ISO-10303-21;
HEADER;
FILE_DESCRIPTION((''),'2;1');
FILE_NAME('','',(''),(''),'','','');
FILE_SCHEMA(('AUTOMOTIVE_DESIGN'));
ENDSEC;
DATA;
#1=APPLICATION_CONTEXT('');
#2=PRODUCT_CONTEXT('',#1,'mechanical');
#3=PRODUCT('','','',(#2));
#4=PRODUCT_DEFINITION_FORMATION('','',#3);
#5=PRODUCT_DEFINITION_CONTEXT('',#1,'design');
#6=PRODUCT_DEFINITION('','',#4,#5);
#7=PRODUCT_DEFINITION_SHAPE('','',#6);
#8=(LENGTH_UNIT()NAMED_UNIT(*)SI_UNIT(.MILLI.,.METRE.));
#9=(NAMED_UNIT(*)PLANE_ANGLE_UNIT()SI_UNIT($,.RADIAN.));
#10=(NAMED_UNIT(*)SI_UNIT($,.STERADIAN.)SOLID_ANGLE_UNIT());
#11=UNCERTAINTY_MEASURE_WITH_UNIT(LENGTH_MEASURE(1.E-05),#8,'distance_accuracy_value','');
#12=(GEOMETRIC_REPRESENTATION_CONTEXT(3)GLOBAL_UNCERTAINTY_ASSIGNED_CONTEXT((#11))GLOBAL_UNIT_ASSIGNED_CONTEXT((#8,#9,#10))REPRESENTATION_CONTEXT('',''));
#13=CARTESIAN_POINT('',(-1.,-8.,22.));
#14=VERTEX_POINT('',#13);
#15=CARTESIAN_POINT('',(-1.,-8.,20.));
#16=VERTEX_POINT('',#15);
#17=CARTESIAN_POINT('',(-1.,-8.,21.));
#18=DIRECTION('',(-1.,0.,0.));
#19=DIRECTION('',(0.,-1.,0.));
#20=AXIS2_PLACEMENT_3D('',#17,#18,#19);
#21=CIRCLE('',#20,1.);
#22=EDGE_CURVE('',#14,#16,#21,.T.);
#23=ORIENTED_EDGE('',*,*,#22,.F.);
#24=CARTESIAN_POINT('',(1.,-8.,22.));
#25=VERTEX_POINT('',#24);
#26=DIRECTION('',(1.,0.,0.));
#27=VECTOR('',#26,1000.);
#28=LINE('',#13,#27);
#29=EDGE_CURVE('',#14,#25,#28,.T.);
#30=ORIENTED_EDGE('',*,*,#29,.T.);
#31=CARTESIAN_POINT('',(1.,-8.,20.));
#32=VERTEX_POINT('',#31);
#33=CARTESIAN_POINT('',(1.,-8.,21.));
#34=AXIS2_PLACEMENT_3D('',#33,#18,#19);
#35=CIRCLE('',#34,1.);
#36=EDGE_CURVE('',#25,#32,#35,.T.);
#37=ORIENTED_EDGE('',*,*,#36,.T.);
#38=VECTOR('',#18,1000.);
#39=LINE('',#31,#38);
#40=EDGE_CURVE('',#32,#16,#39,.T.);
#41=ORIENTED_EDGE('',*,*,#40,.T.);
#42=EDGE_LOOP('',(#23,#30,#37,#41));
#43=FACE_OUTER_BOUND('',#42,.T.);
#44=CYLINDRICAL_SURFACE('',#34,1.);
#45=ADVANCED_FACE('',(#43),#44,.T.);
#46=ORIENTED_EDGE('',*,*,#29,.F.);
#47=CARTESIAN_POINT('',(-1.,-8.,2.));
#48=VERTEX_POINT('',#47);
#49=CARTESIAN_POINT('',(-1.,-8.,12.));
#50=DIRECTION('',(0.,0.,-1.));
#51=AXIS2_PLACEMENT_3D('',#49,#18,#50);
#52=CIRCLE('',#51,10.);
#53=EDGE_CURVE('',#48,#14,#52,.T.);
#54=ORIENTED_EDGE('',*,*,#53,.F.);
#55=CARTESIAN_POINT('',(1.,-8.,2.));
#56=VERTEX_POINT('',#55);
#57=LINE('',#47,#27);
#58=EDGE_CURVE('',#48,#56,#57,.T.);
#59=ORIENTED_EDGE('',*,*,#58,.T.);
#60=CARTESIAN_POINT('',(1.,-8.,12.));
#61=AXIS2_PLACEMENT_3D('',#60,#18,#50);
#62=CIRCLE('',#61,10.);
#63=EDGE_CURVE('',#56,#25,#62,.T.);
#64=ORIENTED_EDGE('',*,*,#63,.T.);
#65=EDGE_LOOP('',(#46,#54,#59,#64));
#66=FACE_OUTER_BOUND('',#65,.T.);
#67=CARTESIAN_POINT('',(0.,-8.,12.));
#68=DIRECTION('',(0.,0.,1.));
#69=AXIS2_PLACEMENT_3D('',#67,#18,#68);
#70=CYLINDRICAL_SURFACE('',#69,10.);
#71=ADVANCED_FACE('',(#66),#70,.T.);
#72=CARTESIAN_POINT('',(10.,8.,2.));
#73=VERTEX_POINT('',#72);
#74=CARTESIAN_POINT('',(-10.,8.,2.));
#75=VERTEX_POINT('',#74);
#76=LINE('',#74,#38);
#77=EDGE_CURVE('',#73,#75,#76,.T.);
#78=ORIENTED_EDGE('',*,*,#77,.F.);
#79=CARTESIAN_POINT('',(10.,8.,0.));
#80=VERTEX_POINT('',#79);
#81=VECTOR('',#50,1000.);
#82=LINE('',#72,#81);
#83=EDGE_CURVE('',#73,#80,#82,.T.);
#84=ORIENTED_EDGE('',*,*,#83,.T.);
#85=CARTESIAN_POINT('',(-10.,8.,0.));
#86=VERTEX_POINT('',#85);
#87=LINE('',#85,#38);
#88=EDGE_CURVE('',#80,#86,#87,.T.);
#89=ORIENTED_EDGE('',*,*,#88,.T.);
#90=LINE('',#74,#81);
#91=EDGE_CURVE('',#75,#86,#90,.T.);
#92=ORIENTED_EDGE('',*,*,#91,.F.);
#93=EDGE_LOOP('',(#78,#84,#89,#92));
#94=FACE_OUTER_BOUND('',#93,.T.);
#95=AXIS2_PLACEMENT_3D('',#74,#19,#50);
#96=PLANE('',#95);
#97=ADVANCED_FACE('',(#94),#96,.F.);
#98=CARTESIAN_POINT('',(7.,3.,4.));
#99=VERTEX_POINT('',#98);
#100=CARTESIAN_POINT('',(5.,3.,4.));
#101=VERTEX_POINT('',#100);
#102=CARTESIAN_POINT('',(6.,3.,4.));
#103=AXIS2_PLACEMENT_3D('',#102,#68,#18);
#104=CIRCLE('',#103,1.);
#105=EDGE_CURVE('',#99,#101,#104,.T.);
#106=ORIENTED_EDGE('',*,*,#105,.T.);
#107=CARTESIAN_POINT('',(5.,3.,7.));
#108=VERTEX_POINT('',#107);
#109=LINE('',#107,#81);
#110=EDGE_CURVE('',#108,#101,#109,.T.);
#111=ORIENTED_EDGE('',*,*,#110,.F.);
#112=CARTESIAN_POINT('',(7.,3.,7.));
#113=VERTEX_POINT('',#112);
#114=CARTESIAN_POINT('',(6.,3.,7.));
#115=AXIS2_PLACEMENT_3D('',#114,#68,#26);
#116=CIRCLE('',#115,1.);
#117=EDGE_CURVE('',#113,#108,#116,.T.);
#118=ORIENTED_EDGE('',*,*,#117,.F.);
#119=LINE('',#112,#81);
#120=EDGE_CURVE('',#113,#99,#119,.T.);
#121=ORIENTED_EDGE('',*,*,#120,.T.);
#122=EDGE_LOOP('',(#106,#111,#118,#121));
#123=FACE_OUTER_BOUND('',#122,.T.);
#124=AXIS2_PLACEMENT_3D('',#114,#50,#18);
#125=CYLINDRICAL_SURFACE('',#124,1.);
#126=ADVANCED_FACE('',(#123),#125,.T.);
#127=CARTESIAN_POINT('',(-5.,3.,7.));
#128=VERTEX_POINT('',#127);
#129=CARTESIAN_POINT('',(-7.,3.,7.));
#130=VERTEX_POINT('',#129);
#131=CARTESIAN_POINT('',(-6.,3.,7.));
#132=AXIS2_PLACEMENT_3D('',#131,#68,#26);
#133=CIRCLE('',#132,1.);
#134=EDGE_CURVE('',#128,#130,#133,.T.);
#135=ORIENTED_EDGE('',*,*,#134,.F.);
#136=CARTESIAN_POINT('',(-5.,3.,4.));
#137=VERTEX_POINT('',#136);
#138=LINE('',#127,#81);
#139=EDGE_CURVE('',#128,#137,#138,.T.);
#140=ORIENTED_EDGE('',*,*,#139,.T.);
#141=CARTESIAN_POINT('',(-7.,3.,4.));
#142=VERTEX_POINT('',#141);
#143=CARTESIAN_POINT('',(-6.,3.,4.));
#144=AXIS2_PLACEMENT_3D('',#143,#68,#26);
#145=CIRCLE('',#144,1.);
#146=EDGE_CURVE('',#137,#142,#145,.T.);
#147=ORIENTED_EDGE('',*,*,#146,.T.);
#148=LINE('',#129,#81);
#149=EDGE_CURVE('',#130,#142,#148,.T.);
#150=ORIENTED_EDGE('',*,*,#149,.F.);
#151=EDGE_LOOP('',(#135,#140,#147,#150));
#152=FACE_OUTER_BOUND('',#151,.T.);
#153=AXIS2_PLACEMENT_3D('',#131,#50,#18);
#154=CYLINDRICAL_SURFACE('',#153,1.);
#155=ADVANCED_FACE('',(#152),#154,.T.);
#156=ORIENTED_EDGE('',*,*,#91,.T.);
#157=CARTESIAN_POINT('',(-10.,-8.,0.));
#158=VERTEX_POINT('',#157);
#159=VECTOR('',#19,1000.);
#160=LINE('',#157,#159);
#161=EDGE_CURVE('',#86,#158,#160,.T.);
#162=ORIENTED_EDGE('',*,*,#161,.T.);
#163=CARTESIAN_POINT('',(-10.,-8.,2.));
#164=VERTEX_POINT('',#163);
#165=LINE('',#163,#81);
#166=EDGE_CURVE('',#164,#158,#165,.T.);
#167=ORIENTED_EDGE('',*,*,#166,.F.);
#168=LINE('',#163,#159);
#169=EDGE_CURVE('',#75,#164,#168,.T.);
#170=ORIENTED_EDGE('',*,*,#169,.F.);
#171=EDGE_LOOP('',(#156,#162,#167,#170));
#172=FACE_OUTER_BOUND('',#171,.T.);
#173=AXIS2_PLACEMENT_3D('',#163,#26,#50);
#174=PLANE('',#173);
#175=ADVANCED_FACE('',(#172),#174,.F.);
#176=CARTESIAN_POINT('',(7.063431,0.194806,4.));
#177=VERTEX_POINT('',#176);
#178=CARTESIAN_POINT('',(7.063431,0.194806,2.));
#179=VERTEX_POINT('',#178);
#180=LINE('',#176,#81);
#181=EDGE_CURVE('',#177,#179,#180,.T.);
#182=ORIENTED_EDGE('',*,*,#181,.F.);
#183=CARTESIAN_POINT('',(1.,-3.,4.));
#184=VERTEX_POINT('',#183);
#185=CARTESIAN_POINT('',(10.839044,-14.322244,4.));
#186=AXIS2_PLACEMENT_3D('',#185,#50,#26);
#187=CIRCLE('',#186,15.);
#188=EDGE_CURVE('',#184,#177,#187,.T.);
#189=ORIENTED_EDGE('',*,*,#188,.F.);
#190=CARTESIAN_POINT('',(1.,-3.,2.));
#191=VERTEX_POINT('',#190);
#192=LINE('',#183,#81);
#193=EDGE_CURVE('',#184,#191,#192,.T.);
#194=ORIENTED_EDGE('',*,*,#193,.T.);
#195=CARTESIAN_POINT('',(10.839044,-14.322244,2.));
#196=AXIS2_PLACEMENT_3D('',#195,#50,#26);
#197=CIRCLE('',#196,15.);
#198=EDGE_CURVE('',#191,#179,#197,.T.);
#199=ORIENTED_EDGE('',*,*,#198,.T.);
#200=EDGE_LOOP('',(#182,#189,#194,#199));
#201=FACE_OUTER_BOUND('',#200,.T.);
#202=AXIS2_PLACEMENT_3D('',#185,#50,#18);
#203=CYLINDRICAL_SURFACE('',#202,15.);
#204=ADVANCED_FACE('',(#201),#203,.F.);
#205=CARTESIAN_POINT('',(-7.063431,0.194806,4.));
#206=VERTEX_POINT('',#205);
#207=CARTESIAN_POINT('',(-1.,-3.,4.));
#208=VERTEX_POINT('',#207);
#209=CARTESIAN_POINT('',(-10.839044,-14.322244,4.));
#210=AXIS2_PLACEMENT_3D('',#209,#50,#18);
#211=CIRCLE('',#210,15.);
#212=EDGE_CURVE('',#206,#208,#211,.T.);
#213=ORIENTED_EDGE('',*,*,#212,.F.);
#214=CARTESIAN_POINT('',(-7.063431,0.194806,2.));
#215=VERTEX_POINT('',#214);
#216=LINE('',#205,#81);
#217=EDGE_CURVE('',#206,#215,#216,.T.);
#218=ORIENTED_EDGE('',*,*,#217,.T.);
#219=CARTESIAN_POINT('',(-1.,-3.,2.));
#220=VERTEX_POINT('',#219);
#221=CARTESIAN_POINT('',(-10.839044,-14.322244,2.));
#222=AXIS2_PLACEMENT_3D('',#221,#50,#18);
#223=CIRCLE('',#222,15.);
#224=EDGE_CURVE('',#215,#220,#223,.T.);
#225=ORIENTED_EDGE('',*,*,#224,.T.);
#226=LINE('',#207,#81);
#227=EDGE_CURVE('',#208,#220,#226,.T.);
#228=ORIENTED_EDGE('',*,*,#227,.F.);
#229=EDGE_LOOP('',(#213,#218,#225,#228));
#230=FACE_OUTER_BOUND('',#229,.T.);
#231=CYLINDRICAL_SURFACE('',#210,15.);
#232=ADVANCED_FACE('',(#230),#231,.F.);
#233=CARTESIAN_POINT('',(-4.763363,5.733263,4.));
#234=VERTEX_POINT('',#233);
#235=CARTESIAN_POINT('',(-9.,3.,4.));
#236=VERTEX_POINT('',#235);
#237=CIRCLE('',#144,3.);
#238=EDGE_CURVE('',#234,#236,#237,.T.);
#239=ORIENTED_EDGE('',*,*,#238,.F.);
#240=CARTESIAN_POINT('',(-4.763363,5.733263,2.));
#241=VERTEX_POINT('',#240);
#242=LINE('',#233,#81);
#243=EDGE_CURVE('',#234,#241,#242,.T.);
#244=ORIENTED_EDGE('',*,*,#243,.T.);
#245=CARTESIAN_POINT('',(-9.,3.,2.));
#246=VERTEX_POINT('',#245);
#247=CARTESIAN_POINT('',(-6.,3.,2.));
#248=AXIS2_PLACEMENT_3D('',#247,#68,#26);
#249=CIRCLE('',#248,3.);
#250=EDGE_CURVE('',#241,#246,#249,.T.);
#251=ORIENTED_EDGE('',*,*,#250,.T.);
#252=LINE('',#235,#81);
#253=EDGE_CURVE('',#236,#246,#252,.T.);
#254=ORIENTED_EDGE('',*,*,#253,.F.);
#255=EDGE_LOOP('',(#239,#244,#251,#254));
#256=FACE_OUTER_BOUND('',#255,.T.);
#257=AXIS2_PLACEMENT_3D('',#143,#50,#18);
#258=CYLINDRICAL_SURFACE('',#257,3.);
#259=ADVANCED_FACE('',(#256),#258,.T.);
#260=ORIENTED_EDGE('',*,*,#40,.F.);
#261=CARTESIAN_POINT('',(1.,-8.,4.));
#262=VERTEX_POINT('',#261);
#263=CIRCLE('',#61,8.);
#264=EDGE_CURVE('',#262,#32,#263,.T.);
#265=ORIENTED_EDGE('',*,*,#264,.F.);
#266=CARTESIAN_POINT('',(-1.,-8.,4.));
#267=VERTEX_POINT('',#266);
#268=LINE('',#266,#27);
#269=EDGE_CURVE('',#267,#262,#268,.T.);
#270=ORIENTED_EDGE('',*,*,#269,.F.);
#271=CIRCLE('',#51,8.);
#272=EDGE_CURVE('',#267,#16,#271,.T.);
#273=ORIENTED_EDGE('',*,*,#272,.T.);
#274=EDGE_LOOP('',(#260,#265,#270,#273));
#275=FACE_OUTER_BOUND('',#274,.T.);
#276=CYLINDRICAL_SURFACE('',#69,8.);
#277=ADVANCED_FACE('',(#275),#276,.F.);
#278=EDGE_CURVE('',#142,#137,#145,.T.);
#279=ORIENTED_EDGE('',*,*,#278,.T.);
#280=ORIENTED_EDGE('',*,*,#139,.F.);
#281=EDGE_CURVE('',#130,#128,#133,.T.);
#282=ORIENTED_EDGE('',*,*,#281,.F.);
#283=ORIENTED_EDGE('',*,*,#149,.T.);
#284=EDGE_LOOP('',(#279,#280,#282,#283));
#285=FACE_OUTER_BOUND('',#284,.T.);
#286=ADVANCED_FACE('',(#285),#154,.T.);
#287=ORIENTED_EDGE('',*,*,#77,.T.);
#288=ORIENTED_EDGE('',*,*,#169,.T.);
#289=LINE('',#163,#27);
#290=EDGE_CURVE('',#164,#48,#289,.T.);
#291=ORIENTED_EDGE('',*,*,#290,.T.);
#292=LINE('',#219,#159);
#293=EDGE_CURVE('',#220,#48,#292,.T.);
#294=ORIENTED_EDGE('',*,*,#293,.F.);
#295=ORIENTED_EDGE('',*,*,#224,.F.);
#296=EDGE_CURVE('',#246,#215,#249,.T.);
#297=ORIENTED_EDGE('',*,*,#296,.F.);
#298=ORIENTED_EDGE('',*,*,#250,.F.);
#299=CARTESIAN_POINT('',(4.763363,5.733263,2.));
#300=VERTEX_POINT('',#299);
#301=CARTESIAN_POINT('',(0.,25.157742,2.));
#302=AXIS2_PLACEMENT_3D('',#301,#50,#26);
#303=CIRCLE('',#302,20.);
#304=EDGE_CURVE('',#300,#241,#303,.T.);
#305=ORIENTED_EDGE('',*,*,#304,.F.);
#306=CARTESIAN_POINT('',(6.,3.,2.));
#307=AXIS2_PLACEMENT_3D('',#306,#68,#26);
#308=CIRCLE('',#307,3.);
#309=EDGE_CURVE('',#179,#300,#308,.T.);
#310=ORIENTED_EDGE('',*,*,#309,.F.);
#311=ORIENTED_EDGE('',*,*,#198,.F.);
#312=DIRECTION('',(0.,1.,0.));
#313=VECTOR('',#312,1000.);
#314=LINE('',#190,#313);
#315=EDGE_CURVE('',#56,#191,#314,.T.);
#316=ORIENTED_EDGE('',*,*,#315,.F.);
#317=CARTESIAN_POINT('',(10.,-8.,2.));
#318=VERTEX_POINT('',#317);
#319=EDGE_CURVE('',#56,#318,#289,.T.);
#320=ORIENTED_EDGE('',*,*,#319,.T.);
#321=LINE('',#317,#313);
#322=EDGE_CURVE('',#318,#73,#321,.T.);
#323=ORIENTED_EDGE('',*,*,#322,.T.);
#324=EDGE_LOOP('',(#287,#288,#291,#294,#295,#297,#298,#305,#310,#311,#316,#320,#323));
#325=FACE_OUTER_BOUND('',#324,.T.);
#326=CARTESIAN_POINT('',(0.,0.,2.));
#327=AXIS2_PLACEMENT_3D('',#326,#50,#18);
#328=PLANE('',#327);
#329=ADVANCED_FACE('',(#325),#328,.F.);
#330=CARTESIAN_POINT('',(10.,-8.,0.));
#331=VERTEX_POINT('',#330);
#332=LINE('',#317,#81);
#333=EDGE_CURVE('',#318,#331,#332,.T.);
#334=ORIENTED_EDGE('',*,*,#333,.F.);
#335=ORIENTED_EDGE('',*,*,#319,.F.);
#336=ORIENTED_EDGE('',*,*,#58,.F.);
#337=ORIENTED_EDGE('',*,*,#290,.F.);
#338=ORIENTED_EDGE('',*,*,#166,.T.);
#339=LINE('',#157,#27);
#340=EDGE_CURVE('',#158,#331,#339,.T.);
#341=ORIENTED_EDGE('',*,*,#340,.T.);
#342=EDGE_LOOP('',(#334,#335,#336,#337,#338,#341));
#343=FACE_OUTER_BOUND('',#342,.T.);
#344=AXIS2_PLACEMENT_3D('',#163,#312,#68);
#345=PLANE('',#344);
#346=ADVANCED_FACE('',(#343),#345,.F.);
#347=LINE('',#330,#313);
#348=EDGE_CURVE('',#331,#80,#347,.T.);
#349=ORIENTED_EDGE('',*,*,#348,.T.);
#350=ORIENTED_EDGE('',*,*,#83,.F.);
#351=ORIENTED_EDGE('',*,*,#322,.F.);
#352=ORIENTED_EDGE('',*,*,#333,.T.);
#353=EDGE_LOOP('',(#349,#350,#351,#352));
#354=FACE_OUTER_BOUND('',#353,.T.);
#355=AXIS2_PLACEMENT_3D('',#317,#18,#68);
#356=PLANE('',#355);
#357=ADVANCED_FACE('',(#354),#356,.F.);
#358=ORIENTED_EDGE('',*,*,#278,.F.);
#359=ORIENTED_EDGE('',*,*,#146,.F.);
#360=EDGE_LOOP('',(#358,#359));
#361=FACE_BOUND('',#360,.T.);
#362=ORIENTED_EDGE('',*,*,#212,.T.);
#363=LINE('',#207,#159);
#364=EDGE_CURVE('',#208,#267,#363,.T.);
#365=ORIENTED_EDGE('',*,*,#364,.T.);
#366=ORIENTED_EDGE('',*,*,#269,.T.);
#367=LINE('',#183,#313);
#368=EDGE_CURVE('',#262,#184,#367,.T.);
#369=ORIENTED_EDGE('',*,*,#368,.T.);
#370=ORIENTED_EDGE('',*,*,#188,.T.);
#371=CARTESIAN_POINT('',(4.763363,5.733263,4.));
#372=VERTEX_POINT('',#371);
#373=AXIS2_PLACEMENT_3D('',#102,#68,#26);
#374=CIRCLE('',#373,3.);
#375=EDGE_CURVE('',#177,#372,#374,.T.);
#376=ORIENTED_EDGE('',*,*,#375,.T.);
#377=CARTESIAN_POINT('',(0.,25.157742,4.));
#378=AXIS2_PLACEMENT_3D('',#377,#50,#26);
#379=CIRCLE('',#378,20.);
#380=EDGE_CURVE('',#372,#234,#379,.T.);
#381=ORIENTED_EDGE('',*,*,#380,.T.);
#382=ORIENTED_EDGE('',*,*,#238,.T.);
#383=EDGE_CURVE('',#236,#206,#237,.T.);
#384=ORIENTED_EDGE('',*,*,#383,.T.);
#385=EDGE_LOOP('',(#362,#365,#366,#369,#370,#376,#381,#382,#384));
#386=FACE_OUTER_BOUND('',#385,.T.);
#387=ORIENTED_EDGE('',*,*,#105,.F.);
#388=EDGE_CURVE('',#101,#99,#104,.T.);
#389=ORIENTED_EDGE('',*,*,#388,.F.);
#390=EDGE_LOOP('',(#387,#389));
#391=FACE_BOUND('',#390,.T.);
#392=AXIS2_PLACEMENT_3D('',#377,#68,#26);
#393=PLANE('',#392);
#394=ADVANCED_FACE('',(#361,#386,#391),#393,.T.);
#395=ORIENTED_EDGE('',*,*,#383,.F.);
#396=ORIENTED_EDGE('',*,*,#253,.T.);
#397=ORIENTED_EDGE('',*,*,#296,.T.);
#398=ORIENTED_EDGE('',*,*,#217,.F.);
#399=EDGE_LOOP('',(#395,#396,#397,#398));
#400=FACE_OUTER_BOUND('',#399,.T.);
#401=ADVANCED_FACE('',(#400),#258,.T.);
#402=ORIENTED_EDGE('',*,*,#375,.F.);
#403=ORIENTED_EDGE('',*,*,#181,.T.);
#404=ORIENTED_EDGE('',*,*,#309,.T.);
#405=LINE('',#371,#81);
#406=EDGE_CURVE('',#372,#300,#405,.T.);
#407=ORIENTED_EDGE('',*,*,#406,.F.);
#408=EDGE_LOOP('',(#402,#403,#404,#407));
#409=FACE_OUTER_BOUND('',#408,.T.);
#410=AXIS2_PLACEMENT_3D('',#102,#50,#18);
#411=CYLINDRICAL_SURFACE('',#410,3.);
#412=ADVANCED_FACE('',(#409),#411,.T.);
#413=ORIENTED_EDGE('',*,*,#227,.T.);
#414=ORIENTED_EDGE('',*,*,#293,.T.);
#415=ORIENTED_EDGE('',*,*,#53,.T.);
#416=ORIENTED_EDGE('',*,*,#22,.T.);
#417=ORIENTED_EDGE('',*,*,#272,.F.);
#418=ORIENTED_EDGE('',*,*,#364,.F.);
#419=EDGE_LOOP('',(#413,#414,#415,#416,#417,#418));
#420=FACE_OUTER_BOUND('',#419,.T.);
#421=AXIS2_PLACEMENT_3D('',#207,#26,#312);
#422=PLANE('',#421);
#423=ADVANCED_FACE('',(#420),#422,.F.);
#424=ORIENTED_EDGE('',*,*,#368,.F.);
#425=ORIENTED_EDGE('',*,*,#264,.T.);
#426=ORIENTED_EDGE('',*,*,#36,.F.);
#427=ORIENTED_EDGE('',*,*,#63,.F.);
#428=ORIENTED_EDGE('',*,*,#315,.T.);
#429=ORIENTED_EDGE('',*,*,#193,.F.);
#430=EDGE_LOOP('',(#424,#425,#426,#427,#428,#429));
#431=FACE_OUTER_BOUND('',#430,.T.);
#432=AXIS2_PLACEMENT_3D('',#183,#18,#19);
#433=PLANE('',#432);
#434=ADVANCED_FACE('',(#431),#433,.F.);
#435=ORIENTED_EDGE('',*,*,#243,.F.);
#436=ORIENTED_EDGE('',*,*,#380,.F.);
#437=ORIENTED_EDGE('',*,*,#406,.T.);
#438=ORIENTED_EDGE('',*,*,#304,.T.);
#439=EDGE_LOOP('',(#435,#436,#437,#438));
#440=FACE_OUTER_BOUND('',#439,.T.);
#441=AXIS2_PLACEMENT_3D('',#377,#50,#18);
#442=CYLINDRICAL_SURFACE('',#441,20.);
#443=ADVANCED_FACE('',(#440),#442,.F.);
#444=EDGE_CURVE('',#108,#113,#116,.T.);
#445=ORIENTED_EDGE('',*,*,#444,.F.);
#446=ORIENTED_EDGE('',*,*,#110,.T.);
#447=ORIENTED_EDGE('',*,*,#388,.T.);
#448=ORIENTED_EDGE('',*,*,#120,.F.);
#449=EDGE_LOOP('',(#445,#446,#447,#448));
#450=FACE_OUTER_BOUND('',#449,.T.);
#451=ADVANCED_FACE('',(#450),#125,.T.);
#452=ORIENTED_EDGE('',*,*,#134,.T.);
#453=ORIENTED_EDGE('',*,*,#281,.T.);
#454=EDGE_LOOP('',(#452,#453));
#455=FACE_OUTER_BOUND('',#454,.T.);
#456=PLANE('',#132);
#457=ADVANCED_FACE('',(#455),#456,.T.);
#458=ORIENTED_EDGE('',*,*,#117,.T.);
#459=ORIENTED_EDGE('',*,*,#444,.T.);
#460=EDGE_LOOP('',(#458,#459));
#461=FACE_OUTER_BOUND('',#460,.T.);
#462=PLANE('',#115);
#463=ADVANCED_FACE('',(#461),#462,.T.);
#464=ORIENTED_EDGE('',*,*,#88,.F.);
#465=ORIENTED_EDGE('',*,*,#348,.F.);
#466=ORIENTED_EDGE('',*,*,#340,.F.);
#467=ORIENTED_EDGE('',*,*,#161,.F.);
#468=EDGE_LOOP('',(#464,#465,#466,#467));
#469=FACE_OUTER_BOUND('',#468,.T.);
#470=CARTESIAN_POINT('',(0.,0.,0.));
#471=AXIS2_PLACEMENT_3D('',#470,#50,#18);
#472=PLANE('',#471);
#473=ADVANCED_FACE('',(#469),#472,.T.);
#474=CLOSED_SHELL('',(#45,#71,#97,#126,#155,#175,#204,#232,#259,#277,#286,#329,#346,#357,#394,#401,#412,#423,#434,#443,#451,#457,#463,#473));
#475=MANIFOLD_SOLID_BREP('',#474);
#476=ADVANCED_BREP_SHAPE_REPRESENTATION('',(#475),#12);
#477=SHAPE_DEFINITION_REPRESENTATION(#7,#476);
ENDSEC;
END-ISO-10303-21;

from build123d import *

# Parameters (mm, degrees)
BACK_PLATE_SKETCH_W      = 20
BACK_PLATE_SKETCH_H      = 16
BACK_PLATE_16X20X2_DEPTH = 2
BRACKET_PROFILE_SKETCH_R = 1
HOOK_BRACKET_DEPTH       = 2
PIN_CIRCLES_SKETCH_R     = 1
MOUNTING_PINS_2X_DEPTH   = 5
HOOK_SECTION_SKETCH_W    = 2
HOOK_SECTION_SKETCH_H    = 2
HOOK_TIP_DEPTH           = 2


with BuildPart() as part:
    # Back Plate Sketch → Back Plate 16x20x2 (new body)
    with BuildSketch(Plane.XY):
        Rectangle(BACK_PLATE_SKETCH_W, BACK_PLATE_SKETCH_H)
    extrude(amount=BACK_PLATE_16X20X2_DEPTH)

    # Bracket Profile Sketch → Hook Bracket (add)
    with BuildSketch(Plane.XY.offset(2)):
        with BuildLine():
            Line((-1, -3), (-1, -8))
            Line((-1, -8), (1, -8))
            Line((1, -8), (1, -3))
            ThreePointArc((1, -3), (3.84680434, -1.051653316), (7.06343132, 0.19480592))
            ThreePointArc((7.06343132, 0.19480592), (8.770582601, 4.150596389), (4.76336302, 5.73326343))
            ThreePointArc((4.76336302, 5.73326343), (0, 5.15774213), (-4.76336302, 5.73326343))
            ThreePointArc((-4.76336302, 5.73326343), (-8.770582601, 4.150596389), (-7.06343132, 0.19480592))
            ThreePointArc((-7.06343132, 0.19480592), (-3.84680434, -1.051653316), (-1, -3))
        make_face()
        with Locations((-6, 3)):
            Circle(BRACKET_PROFILE_SKETCH_R, mode=Mode.SUBTRACT)
        with Locations(Location((6, 3, 0), (0, 0, 180))):
            Circle(BRACKET_PROFILE_SKETCH_R, mode=Mode.SUBTRACT)
    extrude(amount=HOOK_BRACKET_DEPTH)

    # Pin Circles Sketch → Mounting Pins 2x (add)
    with BuildSketch(Plane.XY.offset(2)):
        with Locations((-6, 3)):
            Circle(PIN_CIRCLES_SKETCH_R)
        with Locations(Location((6, 3, 0), (0, 0, 180))):
            Circle(PIN_CIRCLES_SKETCH_R)
    extrude(amount=MOUNTING_PINS_2X_DEPTH)

    # Hook Arm Sweep: sweep along a path in Hook Path Sketch
    with BuildLine(Plane(origin=(0, 0, 0), x_dir=(0, 0, -1), z_dir=(1, 0, 0))) as hook_arm_sweep_path:
        ThreePointArc((-3, -8), (-12, -17), (-21, -8))
    # Hook Section Sketch → Hook Arm Sweep (sweep)
    with BuildSketch(Plane.XZ.offset(8)):
        with Locations((0, 3)):
            Rectangle(HOOK_SECTION_SKETCH_W, HOOK_SECTION_SKETCH_H)
    sweep(path=hook_arm_sweep_path.line)

    # Hook Tip Sketch → Hook Tip (add)
    with BuildSketch(Plane.ZY.offset(1)):
        with BuildLine():
            Line((20, -8), (22, -8))
            ThreePointArc((22, -8), (21, -7), (20, -8))
        make_face()
    extrude(amount=-HOOK_TIP_DEPTH)


solid = part.part
